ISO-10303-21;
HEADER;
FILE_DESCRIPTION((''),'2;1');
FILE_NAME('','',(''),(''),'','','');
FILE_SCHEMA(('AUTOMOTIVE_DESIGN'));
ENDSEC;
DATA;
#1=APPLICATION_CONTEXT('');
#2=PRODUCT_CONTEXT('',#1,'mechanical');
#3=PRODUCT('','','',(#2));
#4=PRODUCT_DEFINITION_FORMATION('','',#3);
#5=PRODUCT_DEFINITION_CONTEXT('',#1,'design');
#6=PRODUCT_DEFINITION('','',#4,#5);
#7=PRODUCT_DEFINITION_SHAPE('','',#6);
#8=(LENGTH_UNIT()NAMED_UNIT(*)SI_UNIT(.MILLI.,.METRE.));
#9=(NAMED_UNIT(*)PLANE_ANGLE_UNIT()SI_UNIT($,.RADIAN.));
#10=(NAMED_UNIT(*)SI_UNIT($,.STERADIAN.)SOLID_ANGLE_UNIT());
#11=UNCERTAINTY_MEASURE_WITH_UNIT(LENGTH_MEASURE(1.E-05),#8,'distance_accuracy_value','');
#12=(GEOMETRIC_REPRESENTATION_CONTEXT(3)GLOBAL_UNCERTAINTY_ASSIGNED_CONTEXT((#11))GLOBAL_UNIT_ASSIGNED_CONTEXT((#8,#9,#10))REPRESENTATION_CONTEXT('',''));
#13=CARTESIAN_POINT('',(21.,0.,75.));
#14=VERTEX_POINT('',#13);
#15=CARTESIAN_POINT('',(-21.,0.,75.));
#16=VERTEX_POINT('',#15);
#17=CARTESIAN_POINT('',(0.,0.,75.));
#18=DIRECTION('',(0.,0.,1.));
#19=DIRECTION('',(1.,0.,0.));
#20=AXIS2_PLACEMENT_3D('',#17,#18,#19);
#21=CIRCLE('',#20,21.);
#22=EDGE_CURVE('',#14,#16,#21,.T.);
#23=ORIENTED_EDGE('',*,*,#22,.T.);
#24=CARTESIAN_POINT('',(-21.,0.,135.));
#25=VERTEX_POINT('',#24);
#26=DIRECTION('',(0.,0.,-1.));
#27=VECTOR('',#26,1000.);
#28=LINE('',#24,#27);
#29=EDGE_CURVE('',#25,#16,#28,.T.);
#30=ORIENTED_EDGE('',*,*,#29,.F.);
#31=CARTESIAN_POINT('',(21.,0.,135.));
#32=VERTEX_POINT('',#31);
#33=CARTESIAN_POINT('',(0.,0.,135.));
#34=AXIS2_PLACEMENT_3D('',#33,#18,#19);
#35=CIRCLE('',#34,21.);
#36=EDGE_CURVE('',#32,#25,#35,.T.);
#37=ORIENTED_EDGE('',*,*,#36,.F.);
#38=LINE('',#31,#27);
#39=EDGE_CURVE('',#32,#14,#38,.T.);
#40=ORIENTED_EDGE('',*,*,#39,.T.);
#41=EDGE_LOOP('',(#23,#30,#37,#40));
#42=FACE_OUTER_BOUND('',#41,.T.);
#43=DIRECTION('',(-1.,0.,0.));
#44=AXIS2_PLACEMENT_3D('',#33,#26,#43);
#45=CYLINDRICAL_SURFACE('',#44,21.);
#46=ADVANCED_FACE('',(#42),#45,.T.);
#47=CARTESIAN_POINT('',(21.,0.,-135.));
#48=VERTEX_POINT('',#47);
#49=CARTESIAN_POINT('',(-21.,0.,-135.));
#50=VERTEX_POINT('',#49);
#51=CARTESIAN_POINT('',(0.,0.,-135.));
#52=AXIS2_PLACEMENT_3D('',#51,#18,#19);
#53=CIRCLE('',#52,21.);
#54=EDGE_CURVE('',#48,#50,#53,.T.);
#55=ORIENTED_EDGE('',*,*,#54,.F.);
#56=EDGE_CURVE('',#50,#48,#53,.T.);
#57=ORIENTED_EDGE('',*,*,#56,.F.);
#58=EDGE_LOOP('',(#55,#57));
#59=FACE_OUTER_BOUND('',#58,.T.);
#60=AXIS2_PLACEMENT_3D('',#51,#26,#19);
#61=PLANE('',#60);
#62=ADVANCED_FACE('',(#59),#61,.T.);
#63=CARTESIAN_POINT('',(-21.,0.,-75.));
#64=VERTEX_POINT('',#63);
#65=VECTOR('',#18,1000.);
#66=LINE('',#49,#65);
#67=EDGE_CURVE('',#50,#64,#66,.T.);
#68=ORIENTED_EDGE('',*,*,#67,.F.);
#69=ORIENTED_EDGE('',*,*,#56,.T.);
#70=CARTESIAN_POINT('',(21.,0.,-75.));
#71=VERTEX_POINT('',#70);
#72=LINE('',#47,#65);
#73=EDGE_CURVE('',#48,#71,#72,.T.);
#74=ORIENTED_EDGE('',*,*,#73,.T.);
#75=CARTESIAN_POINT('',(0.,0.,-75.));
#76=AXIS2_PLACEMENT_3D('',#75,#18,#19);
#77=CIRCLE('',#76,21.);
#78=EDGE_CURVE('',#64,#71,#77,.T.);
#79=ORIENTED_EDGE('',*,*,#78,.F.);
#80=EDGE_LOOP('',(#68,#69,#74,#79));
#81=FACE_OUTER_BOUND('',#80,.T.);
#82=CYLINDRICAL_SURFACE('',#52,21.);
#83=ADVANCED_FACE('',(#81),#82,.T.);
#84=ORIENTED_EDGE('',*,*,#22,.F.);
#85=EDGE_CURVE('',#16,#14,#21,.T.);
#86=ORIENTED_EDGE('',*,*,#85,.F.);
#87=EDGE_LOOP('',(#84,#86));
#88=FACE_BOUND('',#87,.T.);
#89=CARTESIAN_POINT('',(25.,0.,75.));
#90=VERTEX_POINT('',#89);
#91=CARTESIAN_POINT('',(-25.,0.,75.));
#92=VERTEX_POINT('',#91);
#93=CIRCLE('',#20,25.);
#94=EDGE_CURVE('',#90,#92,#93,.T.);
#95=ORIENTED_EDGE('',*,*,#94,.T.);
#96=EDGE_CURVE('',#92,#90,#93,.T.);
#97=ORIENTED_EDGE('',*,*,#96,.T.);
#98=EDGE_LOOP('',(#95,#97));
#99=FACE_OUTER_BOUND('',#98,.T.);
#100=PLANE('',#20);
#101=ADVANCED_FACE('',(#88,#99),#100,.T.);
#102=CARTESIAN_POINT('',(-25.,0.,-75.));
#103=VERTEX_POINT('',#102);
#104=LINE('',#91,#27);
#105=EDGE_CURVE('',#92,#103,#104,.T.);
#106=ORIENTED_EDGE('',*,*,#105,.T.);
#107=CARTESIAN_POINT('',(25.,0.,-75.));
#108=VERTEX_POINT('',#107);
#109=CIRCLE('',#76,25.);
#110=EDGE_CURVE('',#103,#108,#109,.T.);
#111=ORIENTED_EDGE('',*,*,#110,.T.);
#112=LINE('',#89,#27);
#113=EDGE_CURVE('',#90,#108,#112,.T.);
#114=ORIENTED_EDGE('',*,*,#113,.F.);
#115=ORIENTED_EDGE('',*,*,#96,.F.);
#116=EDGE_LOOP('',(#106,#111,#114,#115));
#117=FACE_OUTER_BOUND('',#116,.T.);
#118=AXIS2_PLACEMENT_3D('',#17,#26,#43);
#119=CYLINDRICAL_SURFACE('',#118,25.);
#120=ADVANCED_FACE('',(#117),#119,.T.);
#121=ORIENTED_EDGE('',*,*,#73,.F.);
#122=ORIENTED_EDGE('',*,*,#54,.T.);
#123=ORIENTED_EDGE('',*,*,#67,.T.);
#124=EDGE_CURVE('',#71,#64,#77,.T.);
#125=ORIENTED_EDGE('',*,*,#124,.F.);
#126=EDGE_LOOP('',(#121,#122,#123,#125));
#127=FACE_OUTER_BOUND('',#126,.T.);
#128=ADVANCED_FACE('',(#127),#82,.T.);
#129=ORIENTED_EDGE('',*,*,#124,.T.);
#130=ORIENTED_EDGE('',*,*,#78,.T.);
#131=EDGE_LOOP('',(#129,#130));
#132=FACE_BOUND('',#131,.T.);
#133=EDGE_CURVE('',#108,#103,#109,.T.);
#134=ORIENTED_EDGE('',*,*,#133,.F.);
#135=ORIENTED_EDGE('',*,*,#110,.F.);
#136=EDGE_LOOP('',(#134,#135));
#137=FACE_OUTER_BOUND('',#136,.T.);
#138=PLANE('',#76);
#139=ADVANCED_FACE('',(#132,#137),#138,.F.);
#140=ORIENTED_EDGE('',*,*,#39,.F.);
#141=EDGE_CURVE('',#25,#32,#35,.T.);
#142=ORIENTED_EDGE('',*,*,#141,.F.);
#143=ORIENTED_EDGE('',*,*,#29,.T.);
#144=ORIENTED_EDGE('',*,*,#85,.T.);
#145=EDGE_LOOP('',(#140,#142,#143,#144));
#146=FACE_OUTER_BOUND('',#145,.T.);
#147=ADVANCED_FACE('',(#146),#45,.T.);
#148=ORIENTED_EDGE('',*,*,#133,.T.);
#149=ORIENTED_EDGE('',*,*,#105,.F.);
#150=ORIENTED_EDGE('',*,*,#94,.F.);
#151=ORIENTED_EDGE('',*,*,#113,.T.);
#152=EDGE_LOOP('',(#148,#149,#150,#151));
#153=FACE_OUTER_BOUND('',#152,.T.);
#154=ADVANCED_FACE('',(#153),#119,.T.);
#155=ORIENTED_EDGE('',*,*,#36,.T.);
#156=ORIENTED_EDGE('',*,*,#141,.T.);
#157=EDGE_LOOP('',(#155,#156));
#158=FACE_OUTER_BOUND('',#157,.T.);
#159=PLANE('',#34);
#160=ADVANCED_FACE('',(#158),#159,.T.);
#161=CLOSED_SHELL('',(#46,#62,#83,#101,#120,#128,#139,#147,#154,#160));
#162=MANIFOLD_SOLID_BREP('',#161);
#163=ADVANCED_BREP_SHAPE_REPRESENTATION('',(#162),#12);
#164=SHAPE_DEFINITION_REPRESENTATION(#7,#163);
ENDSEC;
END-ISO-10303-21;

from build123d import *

# Parameters (mm, degrees)
SKETCH_1_R           = 25
BOSS_EXTRUDE_1_DEPTH = 75
SKETCH_2_R           = 21
BOSS_EXTRUDE_2_DEPTH = 60


with BuildPart() as part:
    # Sketch 1 → Boss-Extrude 1 (new, symmetric)
    with BuildSketch(Plane.XY):
        Circle(SKETCH_1_R)
    extrude(amount=BOSS_EXTRUDE_1_DEPTH, both=True)

    # Sketch 2 → Boss-Extrude 2 (add)
    with BuildSketch(Plane.XY.offset(75)):
        Circle(SKETCH_2_R)
    boss_extrude_2 = extrude(amount=BOSS_EXTRUDE_2_DEPTH)

    # Mirror 1: Boss-Extrude 2 across plane
    add(boss_extrude_2.mirror(Plane.XY))


solid = part.part
